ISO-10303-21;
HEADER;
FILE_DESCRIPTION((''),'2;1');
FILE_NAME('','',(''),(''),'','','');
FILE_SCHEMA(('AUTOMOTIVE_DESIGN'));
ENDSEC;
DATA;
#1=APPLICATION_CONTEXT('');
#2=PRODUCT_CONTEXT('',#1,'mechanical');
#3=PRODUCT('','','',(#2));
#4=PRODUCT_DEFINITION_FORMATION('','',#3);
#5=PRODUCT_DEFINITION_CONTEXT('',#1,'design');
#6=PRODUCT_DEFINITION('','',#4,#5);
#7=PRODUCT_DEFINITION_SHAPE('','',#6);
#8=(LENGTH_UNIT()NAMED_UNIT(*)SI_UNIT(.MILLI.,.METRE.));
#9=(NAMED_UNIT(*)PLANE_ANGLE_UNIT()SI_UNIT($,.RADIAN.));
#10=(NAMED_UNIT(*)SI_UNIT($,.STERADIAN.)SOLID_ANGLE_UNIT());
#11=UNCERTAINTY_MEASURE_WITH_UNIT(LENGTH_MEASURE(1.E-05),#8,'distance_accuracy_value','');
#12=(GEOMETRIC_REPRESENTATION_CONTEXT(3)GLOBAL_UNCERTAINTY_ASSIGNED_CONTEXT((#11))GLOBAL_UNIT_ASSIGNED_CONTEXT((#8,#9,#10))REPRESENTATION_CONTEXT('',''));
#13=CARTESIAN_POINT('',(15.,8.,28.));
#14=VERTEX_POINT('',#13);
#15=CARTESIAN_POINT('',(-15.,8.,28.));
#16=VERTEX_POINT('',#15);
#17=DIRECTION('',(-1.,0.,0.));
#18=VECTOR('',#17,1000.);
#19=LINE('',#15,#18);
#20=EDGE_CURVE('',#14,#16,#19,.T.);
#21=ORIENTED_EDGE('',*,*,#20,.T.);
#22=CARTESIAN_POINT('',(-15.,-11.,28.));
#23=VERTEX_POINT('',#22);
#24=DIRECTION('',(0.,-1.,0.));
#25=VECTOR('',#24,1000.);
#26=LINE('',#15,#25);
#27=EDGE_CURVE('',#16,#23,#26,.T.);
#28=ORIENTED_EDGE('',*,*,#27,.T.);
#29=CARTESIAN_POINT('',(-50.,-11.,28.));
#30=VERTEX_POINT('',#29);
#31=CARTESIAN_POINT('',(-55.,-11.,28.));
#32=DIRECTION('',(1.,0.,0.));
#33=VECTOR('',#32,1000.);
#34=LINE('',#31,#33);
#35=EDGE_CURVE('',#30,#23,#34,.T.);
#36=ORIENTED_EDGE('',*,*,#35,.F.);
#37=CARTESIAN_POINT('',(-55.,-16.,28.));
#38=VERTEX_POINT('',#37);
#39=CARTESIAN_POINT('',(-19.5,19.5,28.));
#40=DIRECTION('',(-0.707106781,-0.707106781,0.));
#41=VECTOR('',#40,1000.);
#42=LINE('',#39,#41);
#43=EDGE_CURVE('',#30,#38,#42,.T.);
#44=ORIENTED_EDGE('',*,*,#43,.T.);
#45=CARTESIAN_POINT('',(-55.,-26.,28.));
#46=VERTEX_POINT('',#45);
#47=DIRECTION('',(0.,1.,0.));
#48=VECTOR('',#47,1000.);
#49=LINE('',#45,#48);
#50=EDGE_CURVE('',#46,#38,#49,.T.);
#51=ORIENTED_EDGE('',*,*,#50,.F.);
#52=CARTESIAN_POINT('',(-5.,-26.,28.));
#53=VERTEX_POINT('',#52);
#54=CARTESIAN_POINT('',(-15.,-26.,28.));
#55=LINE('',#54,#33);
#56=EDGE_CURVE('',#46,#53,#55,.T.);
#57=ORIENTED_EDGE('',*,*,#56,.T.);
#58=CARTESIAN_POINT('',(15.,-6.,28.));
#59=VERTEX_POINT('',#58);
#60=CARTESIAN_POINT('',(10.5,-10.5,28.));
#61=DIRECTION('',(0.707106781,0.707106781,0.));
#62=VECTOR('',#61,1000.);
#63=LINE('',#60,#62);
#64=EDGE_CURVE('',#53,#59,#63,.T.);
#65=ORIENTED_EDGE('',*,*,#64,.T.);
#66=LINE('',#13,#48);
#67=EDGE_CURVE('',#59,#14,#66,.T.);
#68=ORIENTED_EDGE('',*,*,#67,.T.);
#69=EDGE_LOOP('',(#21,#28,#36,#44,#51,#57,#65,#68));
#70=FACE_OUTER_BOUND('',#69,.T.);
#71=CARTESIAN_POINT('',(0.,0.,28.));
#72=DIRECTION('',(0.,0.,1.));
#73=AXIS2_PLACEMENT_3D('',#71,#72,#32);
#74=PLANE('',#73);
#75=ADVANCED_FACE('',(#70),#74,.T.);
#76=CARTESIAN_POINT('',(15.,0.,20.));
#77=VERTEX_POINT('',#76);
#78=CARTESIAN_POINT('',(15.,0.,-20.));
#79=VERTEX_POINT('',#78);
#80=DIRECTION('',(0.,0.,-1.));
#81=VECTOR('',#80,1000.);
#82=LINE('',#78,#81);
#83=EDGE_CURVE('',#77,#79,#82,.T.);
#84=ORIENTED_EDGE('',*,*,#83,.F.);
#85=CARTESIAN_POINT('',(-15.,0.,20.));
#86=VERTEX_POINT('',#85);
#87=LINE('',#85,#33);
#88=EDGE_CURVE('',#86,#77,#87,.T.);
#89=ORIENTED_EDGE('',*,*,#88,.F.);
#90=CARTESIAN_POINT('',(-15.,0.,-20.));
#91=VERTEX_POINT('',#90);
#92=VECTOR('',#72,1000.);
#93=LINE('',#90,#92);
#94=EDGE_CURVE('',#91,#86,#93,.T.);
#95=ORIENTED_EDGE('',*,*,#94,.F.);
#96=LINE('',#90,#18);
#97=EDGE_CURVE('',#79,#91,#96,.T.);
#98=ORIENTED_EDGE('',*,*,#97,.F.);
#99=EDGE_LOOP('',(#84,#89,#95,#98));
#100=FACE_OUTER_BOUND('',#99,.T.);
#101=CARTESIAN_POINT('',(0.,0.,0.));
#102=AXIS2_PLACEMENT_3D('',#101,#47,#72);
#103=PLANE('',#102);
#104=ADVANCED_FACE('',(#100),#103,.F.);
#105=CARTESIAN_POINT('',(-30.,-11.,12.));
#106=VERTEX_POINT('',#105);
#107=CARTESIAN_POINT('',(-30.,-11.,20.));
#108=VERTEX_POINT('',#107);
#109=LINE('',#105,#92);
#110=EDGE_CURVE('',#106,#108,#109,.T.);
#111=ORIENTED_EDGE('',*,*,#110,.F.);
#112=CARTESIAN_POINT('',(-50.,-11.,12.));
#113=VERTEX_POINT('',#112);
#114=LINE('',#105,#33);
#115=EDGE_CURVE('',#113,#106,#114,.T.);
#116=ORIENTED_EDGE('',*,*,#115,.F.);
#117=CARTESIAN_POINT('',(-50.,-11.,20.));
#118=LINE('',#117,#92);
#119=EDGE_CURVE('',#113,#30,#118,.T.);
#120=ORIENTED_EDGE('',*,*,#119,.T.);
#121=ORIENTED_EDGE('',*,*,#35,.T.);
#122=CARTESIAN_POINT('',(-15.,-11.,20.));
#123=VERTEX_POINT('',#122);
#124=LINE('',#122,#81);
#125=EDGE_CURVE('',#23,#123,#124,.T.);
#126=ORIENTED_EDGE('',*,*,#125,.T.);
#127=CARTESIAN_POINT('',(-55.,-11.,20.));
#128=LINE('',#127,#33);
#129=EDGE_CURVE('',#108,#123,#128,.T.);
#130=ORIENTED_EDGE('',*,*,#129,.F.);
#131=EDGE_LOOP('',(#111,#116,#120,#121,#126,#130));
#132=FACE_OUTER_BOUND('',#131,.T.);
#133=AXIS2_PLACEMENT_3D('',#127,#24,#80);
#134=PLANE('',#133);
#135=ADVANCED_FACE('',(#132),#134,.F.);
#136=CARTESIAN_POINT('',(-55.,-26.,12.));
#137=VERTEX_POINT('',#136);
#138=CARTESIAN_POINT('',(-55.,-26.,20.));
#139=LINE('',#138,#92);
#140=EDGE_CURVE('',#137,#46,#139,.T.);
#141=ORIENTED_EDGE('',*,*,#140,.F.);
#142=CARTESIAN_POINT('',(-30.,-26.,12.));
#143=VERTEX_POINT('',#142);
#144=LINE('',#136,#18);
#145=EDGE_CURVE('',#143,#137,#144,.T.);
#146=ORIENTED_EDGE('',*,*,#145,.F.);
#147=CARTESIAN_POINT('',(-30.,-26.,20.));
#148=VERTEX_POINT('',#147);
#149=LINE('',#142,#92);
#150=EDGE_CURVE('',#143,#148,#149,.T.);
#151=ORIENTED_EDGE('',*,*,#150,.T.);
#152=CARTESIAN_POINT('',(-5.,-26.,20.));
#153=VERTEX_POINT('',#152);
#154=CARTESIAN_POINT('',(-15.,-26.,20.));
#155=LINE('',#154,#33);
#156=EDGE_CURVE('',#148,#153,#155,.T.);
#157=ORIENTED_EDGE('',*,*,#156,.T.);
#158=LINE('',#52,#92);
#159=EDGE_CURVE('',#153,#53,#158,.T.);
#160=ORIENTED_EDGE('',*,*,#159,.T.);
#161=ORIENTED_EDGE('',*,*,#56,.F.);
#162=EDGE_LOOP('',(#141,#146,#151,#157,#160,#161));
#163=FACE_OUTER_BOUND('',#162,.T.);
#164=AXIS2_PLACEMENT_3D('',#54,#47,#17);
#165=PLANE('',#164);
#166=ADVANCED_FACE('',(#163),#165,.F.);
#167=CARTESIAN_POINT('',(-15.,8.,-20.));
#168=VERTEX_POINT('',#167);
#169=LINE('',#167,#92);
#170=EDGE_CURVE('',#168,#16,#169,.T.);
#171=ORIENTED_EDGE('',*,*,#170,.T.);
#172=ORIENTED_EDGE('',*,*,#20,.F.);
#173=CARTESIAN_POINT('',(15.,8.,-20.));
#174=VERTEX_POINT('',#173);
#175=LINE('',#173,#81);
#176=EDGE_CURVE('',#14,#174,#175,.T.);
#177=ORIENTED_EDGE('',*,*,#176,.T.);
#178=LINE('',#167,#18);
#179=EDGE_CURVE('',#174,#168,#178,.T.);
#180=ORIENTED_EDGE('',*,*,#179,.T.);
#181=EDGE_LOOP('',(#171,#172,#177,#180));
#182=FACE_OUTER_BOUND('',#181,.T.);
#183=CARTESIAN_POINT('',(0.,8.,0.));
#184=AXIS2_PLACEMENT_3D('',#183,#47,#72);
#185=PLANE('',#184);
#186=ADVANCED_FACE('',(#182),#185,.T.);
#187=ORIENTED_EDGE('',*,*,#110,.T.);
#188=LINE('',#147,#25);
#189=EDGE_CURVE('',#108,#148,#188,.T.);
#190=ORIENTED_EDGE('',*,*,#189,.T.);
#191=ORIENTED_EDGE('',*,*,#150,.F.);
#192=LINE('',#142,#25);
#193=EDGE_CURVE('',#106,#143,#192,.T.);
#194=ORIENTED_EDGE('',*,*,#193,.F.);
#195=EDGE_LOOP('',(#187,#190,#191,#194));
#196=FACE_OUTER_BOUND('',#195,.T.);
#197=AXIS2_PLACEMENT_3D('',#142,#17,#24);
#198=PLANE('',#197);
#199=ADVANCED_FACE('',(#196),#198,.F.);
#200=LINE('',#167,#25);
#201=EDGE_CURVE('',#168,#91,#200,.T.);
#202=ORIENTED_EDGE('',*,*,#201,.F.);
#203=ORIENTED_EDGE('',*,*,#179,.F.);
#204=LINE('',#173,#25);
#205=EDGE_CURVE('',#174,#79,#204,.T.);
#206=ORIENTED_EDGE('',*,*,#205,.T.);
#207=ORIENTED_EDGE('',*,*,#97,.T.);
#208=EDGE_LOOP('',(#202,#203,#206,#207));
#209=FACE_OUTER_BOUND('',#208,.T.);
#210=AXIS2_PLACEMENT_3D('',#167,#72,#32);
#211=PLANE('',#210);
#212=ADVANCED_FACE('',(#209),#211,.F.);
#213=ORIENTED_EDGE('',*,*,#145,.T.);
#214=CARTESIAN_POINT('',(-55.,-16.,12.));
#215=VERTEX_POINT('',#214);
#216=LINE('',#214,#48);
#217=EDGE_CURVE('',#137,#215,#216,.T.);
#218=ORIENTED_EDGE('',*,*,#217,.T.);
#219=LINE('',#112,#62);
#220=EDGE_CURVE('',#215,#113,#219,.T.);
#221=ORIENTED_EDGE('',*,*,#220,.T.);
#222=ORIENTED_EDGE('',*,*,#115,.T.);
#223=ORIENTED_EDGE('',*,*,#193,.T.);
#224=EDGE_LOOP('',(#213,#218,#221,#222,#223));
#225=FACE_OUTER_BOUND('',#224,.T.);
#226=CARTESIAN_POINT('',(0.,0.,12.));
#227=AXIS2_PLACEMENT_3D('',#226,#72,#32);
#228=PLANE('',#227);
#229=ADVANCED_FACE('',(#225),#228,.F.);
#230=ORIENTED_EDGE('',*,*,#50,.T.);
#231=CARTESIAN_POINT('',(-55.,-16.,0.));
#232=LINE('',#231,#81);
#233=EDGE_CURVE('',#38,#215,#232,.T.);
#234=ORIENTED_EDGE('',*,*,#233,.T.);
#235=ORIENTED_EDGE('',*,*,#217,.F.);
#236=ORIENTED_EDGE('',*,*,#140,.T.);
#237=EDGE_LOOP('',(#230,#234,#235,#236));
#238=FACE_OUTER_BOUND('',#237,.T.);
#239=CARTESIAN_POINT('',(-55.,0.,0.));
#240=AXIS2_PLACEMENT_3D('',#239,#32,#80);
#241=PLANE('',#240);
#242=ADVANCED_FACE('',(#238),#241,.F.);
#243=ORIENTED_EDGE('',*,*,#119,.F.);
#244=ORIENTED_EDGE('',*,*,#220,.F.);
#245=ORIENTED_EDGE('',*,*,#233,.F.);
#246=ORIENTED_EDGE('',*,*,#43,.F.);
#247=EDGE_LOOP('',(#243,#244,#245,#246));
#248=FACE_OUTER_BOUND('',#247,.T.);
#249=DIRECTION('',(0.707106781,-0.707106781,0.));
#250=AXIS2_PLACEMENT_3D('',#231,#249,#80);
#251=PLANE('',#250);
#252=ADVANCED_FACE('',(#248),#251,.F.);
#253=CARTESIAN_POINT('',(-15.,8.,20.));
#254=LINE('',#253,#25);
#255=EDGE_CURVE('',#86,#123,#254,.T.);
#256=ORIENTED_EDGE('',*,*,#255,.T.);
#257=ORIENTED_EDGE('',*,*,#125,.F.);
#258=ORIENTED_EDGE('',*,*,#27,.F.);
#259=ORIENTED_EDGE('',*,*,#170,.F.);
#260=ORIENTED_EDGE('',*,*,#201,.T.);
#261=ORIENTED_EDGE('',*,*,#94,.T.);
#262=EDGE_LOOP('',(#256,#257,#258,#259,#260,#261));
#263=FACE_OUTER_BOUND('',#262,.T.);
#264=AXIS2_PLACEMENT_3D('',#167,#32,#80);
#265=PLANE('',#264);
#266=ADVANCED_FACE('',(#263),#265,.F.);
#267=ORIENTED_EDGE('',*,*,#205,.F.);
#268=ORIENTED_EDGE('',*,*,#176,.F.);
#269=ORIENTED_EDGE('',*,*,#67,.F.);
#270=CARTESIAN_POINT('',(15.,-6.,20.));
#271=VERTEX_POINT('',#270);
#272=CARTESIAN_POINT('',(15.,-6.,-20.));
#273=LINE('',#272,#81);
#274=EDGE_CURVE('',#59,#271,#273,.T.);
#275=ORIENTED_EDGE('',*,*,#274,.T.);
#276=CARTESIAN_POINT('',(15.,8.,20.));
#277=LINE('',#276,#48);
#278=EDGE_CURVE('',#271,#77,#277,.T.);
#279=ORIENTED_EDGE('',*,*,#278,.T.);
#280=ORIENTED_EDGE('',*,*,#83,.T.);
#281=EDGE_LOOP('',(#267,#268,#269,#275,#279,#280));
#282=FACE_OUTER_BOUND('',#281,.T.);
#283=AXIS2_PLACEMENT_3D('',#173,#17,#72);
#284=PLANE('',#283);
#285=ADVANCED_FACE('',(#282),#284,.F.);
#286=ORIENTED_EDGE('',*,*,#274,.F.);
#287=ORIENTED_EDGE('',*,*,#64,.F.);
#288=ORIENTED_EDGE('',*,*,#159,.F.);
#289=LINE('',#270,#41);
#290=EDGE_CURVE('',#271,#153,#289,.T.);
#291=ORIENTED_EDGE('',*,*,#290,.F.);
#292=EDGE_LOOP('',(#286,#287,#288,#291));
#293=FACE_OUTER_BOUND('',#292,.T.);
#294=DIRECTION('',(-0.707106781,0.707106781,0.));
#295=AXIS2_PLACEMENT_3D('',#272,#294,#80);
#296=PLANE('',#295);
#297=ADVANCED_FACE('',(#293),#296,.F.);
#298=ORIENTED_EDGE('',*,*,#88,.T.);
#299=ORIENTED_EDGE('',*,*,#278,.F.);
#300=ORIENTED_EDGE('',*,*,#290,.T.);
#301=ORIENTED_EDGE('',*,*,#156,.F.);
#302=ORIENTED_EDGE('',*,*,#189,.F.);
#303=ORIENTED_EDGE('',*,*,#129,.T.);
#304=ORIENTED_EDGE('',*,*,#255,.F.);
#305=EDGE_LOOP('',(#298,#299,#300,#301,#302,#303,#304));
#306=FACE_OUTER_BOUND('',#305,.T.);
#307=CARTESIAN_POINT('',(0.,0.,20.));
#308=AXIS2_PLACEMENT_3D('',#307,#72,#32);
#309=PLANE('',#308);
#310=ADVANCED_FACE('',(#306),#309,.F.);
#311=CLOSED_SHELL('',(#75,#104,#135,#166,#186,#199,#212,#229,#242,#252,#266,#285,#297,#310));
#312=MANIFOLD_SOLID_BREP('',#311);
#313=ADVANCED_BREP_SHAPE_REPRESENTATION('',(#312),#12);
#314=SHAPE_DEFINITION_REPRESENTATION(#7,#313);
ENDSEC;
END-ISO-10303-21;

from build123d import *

# Parameters (mm, degrees)
SKETCH1_W           = 30
SKETCH1_H           = 40
BOSS_EXTRUDE1_DEPTH = 8
SKETCH2_W           = 30
SKETCH2_H           = 34
BOSS_EXTRUDE2_DEPTH = 8
SKETCH3_W           = 8
SKETCH3_H           = 15
BOSS_EXTRUDE3_DEPTH = 40
CHAMFER1_SIZE       = 5
BOSS_EXTRUDE4_DEPTH = 8
CHAMFER2_SIZE       = 20


with BuildPart() as part:
    # Sketch1 → Boss-Extrude1 (new body)
    with BuildSketch(Plane(origin=(0, 0, 0), x_dir=(1, 0, 0), z_dir=(0, 1, 0))):
        Rectangle(SKETCH1_W, SKETCH1_H)
    extrude(amount=BOSS_EXTRUDE1_DEPTH)

    # Sketch2 → Boss-Extrude2 (add)
    with BuildSketch(Plane.XY.offset(20)):
        with Locations((0, -9)):
            Rectangle(SKETCH2_W, SKETCH2_H)
    extrude(amount=BOSS_EXTRUDE2_DEPTH)

    # Sketch3 → Boss-Extrude3 (add)
    with BuildSketch(Plane.ZY.offset(15)):
        with Locations((24, -18.5)):
            Rectangle(SKETCH3_W, SKETCH3_H)
    extrude(amount=BOSS_EXTRUDE3_DEPTH)

    # Chamfer1
    chamfer1_edges = [part.edges().sort_by_distance(p)[0] for p in [
        (-55, -11, 24),
    ]]
    chamfer(chamfer1_edges, length=CHAMFER1_SIZE)

    # Sketch4 → Boss-Extrude4 (add)
    with BuildSketch(Plane(origin=(0, 0, 20), x_dir=(-1, 0, 0), z_dir=(0, 0, -1))):
        Polygon((30, -11), (50, -11), (55, -16), (55, -26), (30, -26), align=None)
    extrude(amount=BOSS_EXTRUDE4_DEPTH)

    # Chamfer2
    chamfer2_edges = [part.edges().sort_by_distance(p)[0] for p in [
        (15, -26, 24),
    ]]
    chamfer(chamfer2_edges, length=CHAMFER2_SIZE)


solid = part.part
